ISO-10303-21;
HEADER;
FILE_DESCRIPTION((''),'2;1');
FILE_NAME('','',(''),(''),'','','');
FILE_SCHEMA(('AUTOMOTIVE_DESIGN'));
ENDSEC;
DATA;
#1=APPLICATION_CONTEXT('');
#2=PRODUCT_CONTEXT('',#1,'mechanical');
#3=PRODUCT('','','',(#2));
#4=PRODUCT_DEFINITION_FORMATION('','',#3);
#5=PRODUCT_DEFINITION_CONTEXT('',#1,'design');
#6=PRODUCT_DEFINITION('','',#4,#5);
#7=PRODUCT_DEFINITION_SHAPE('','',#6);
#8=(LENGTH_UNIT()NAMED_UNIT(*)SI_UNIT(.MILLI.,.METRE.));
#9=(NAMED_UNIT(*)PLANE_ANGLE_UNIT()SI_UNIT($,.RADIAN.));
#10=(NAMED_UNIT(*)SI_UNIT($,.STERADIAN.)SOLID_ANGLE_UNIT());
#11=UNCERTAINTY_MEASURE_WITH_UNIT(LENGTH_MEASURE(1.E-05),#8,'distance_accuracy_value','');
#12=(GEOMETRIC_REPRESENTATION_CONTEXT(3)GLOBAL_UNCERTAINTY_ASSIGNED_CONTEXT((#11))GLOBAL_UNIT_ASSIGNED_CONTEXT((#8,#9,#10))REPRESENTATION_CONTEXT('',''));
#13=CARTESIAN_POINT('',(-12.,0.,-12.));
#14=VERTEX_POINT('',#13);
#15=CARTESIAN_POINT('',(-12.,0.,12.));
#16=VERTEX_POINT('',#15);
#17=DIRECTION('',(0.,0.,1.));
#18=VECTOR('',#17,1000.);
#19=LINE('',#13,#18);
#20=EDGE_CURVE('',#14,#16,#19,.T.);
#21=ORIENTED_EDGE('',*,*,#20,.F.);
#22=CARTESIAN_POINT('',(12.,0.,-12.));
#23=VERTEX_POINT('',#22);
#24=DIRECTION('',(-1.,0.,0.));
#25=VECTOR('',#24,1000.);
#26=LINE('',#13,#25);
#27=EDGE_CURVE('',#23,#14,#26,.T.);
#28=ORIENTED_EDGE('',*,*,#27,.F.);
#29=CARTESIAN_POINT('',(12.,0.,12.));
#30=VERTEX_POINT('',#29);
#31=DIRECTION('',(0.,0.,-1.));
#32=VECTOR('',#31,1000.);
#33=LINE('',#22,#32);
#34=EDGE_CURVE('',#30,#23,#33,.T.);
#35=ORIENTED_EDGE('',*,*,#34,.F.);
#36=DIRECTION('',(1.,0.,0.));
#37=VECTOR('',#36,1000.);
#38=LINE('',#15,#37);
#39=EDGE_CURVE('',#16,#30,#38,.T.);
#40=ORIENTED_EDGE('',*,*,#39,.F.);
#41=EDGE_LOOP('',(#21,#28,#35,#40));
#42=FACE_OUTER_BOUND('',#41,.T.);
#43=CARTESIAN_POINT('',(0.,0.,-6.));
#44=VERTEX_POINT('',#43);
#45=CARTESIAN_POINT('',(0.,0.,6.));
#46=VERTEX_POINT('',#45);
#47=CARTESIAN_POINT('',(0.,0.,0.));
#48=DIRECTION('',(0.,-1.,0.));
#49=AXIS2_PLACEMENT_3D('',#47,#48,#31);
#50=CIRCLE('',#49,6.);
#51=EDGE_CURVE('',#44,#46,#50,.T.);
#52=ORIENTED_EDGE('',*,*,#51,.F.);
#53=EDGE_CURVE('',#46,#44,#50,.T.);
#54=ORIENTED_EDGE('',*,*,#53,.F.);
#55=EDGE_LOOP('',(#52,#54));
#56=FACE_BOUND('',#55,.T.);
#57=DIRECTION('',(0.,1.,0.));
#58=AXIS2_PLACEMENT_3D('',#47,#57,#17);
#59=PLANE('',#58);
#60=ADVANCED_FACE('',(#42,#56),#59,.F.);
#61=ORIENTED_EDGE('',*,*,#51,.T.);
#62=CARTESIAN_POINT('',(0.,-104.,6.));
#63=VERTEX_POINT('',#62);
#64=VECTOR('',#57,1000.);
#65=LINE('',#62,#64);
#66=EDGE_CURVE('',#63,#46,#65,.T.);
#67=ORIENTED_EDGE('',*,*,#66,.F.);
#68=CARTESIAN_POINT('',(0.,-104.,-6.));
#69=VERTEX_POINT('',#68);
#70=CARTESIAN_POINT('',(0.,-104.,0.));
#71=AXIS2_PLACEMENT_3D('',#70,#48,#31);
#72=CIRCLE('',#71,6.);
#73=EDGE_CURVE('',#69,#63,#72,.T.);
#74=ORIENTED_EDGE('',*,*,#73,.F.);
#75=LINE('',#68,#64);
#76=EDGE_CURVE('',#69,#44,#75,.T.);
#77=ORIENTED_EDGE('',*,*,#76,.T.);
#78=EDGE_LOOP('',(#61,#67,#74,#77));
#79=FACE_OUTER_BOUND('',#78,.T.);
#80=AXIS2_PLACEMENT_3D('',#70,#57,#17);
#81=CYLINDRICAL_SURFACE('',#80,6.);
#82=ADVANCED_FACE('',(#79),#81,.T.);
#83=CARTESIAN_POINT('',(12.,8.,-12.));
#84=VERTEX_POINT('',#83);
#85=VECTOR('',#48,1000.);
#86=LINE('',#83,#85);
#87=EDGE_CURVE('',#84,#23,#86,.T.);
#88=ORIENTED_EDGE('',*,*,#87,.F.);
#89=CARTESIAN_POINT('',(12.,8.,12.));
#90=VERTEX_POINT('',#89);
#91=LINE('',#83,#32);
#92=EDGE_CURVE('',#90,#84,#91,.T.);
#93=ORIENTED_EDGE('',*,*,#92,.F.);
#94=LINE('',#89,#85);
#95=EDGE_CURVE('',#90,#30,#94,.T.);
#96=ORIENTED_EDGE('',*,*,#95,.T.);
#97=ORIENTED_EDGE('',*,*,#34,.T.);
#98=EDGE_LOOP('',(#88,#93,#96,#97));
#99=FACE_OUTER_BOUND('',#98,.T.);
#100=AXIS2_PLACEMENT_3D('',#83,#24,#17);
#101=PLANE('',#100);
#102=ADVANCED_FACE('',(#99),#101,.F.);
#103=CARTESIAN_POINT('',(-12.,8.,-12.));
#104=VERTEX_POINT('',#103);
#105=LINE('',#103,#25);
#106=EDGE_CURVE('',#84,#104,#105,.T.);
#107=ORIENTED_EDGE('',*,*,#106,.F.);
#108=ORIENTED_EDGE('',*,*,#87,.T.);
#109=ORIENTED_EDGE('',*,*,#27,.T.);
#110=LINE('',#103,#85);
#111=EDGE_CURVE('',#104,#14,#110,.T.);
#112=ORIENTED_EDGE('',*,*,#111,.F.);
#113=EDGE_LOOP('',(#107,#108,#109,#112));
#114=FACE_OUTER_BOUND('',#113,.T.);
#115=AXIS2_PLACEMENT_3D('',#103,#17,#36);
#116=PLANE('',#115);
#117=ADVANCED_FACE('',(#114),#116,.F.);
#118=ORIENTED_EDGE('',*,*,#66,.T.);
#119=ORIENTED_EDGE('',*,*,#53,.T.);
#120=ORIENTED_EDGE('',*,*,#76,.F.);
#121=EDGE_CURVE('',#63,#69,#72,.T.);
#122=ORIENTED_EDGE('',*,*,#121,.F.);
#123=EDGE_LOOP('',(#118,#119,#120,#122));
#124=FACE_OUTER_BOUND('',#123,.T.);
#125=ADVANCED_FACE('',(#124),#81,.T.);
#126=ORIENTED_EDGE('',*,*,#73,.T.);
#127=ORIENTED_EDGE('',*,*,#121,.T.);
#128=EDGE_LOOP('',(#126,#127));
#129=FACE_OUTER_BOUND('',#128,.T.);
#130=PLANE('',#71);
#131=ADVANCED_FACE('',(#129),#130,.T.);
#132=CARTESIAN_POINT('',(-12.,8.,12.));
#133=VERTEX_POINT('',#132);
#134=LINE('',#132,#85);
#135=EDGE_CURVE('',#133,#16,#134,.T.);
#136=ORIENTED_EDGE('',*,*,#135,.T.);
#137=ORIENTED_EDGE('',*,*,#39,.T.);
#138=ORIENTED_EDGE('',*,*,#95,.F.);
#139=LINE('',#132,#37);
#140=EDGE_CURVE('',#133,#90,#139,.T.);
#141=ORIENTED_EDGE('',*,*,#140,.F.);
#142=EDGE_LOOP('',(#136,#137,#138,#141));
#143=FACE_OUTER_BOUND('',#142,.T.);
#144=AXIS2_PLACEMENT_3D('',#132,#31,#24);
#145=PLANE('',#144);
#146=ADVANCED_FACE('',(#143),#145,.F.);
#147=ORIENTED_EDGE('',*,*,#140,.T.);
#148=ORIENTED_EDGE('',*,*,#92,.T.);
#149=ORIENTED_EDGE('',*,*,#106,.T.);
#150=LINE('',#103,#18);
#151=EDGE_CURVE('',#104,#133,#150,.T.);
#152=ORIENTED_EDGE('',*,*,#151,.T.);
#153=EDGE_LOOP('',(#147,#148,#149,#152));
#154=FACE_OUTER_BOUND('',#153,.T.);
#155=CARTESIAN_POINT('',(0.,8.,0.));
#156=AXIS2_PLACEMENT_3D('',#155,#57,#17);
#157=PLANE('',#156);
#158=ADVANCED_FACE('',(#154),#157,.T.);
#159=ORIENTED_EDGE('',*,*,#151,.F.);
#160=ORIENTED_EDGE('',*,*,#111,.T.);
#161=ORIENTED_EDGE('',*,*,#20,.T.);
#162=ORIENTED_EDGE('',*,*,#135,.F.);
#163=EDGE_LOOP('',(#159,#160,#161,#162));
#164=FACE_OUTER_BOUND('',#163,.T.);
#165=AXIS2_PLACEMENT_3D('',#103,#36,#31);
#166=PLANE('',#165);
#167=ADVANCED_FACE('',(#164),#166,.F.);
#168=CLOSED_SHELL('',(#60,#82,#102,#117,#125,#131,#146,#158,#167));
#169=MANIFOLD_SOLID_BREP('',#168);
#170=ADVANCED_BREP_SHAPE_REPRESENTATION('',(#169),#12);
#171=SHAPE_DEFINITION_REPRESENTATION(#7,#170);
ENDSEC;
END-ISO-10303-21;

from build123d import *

# Parameters (mm, degrees)
HEAD_PROFILE_24X24_W      = 24
HEAD_PROFILE_24X24_H      = 24
SQUARE_HEAD_24X24X8_DEPTH = 8
SHANK_PROFILE_12_R        = 6
SHANK_12X104_DEPTH        = 104


with BuildPart() as part:
    # Head Profile 24x24 → Square Head 24x24x8 (new body)
    with BuildSketch(Plane(origin=(0, 0, 0), x_dir=(1, 0, 0), z_dir=(0, 1, 0))):
        Rectangle(HEAD_PROFILE_24X24_W, HEAD_PROFILE_24X24_H)
    extrude(amount=SQUARE_HEAD_24X24X8_DEPTH)

    # Shank Profile Ø12 → Shank Ø12x104 (add)
    with BuildSketch(Plane.XZ):
        with Locations(Location((0, 0, 0), (0, 0, 90))):
            Circle(SHANK_PROFILE_12_R)
    extrude(amount=SHANK_12X104_DEPTH)


solid = part.part
